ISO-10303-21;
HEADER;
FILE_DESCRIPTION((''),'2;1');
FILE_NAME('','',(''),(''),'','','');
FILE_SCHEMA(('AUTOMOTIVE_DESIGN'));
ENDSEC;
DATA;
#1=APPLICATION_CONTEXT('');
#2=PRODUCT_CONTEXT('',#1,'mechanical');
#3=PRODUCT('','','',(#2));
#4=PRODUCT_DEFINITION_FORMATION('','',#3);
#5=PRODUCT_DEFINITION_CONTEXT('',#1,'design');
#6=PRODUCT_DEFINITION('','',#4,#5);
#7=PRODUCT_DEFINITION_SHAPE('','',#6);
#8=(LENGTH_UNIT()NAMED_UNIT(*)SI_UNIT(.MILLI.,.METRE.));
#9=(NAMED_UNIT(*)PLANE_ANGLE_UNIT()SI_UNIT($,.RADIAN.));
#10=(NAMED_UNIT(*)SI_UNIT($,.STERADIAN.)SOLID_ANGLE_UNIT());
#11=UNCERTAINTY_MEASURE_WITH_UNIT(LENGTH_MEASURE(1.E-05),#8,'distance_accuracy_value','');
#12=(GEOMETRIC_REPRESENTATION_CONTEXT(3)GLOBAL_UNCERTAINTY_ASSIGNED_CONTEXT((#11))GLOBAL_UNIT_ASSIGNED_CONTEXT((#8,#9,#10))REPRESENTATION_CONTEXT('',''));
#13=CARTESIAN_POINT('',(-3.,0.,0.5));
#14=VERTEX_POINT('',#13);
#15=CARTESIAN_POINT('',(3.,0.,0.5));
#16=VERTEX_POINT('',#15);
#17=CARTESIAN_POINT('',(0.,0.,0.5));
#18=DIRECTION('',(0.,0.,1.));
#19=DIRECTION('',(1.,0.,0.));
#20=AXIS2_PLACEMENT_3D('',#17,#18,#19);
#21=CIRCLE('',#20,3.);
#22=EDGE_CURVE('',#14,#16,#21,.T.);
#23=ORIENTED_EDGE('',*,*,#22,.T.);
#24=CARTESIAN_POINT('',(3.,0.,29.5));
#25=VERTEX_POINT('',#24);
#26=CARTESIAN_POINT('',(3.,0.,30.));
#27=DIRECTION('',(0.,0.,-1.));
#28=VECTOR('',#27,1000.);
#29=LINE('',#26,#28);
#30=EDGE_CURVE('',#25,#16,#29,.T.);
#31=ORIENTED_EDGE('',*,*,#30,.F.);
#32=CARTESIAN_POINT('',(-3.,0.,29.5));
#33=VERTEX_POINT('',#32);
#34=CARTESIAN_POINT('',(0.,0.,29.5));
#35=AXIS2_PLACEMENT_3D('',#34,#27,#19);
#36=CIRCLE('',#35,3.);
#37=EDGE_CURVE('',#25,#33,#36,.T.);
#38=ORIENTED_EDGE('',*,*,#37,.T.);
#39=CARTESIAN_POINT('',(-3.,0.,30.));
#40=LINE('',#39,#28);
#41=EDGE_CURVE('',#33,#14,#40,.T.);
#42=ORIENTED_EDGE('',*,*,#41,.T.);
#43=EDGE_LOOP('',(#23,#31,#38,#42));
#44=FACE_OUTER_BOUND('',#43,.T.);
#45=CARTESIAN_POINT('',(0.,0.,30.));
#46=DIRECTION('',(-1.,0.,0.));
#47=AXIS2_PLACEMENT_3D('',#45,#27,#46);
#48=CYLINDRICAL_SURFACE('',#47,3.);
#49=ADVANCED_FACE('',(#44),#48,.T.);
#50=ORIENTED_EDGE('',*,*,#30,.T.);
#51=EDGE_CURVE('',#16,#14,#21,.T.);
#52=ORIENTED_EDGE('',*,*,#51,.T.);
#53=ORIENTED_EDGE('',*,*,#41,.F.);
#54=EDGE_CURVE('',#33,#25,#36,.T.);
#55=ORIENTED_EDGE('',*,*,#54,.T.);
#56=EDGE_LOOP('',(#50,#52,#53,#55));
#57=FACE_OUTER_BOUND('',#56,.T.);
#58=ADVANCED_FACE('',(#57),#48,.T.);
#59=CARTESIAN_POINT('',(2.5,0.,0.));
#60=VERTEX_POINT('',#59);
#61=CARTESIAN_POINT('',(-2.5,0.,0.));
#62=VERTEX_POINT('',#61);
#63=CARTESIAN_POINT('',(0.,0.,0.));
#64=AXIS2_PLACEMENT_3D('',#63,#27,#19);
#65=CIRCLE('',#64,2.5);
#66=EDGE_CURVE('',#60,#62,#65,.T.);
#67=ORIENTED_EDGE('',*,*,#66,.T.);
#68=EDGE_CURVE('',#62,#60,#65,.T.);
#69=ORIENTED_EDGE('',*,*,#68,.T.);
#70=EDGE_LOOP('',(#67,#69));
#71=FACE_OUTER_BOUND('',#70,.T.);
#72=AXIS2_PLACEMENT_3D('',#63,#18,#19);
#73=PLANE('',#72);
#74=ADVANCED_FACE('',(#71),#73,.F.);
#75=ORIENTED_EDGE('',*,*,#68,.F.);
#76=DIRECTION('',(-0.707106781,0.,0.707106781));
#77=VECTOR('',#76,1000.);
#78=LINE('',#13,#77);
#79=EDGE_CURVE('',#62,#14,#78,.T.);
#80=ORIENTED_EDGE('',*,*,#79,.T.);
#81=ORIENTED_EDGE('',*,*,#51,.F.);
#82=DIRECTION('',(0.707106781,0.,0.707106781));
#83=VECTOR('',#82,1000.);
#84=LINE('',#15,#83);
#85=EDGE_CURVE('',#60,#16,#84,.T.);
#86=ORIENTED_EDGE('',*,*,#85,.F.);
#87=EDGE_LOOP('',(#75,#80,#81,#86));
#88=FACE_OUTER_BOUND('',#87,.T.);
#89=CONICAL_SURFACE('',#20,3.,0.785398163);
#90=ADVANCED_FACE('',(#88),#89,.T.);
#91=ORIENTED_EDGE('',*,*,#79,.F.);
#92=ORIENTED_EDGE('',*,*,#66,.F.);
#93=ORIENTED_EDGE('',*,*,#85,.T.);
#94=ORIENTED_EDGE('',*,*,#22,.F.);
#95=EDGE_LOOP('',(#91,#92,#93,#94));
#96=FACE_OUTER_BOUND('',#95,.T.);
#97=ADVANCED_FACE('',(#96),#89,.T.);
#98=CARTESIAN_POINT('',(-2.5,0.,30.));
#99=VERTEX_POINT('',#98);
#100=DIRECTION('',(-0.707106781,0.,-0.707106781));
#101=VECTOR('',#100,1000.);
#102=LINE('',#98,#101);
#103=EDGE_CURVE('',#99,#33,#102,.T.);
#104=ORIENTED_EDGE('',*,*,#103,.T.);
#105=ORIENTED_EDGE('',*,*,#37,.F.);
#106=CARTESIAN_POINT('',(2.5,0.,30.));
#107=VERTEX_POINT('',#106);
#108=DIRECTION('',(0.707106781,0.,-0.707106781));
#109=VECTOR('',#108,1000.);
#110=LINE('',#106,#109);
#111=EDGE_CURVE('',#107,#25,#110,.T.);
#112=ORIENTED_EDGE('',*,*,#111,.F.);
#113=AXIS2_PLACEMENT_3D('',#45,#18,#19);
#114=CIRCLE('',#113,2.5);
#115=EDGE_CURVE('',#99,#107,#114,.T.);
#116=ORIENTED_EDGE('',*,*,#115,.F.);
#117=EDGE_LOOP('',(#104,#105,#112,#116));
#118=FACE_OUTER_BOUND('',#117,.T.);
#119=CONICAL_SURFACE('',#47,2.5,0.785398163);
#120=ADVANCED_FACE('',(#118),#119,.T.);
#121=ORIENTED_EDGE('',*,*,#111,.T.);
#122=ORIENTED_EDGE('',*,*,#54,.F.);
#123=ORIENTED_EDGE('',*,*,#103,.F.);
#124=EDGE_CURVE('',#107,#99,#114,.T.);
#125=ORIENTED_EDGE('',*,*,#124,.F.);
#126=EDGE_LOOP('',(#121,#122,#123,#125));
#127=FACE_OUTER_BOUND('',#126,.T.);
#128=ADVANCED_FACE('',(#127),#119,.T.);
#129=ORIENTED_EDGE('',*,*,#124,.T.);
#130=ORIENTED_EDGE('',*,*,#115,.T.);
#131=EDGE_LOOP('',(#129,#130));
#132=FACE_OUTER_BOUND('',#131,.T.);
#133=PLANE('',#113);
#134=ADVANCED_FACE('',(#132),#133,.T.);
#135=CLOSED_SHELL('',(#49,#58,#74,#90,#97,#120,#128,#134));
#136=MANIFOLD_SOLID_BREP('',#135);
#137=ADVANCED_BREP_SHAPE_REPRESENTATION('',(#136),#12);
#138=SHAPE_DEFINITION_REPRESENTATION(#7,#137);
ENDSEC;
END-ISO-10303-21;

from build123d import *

# Parameters (mm, degrees)
SKETCH1_R           = 3
BOSS_EXTRUDE1_DEPTH = 30
CHAMFER1_SIZE       = 0.5


with BuildPart() as part:
    # Sketch1 → Boss-Extrude1 (new body)
    with BuildSketch(Plane.XY):
        Circle(SKETCH1_R)
    extrude(amount=BOSS_EXTRUDE1_DEPTH)

    # Chamfer1
    chamfer1_edges = [part.edges().sort_by_distance(p)[0] for p in [
        (-3, 0, 0),
        (-3, 0, 30),
    ]]
    chamfer(chamfer1_edges, length=CHAMFER1_SIZE)


solid = part.part
